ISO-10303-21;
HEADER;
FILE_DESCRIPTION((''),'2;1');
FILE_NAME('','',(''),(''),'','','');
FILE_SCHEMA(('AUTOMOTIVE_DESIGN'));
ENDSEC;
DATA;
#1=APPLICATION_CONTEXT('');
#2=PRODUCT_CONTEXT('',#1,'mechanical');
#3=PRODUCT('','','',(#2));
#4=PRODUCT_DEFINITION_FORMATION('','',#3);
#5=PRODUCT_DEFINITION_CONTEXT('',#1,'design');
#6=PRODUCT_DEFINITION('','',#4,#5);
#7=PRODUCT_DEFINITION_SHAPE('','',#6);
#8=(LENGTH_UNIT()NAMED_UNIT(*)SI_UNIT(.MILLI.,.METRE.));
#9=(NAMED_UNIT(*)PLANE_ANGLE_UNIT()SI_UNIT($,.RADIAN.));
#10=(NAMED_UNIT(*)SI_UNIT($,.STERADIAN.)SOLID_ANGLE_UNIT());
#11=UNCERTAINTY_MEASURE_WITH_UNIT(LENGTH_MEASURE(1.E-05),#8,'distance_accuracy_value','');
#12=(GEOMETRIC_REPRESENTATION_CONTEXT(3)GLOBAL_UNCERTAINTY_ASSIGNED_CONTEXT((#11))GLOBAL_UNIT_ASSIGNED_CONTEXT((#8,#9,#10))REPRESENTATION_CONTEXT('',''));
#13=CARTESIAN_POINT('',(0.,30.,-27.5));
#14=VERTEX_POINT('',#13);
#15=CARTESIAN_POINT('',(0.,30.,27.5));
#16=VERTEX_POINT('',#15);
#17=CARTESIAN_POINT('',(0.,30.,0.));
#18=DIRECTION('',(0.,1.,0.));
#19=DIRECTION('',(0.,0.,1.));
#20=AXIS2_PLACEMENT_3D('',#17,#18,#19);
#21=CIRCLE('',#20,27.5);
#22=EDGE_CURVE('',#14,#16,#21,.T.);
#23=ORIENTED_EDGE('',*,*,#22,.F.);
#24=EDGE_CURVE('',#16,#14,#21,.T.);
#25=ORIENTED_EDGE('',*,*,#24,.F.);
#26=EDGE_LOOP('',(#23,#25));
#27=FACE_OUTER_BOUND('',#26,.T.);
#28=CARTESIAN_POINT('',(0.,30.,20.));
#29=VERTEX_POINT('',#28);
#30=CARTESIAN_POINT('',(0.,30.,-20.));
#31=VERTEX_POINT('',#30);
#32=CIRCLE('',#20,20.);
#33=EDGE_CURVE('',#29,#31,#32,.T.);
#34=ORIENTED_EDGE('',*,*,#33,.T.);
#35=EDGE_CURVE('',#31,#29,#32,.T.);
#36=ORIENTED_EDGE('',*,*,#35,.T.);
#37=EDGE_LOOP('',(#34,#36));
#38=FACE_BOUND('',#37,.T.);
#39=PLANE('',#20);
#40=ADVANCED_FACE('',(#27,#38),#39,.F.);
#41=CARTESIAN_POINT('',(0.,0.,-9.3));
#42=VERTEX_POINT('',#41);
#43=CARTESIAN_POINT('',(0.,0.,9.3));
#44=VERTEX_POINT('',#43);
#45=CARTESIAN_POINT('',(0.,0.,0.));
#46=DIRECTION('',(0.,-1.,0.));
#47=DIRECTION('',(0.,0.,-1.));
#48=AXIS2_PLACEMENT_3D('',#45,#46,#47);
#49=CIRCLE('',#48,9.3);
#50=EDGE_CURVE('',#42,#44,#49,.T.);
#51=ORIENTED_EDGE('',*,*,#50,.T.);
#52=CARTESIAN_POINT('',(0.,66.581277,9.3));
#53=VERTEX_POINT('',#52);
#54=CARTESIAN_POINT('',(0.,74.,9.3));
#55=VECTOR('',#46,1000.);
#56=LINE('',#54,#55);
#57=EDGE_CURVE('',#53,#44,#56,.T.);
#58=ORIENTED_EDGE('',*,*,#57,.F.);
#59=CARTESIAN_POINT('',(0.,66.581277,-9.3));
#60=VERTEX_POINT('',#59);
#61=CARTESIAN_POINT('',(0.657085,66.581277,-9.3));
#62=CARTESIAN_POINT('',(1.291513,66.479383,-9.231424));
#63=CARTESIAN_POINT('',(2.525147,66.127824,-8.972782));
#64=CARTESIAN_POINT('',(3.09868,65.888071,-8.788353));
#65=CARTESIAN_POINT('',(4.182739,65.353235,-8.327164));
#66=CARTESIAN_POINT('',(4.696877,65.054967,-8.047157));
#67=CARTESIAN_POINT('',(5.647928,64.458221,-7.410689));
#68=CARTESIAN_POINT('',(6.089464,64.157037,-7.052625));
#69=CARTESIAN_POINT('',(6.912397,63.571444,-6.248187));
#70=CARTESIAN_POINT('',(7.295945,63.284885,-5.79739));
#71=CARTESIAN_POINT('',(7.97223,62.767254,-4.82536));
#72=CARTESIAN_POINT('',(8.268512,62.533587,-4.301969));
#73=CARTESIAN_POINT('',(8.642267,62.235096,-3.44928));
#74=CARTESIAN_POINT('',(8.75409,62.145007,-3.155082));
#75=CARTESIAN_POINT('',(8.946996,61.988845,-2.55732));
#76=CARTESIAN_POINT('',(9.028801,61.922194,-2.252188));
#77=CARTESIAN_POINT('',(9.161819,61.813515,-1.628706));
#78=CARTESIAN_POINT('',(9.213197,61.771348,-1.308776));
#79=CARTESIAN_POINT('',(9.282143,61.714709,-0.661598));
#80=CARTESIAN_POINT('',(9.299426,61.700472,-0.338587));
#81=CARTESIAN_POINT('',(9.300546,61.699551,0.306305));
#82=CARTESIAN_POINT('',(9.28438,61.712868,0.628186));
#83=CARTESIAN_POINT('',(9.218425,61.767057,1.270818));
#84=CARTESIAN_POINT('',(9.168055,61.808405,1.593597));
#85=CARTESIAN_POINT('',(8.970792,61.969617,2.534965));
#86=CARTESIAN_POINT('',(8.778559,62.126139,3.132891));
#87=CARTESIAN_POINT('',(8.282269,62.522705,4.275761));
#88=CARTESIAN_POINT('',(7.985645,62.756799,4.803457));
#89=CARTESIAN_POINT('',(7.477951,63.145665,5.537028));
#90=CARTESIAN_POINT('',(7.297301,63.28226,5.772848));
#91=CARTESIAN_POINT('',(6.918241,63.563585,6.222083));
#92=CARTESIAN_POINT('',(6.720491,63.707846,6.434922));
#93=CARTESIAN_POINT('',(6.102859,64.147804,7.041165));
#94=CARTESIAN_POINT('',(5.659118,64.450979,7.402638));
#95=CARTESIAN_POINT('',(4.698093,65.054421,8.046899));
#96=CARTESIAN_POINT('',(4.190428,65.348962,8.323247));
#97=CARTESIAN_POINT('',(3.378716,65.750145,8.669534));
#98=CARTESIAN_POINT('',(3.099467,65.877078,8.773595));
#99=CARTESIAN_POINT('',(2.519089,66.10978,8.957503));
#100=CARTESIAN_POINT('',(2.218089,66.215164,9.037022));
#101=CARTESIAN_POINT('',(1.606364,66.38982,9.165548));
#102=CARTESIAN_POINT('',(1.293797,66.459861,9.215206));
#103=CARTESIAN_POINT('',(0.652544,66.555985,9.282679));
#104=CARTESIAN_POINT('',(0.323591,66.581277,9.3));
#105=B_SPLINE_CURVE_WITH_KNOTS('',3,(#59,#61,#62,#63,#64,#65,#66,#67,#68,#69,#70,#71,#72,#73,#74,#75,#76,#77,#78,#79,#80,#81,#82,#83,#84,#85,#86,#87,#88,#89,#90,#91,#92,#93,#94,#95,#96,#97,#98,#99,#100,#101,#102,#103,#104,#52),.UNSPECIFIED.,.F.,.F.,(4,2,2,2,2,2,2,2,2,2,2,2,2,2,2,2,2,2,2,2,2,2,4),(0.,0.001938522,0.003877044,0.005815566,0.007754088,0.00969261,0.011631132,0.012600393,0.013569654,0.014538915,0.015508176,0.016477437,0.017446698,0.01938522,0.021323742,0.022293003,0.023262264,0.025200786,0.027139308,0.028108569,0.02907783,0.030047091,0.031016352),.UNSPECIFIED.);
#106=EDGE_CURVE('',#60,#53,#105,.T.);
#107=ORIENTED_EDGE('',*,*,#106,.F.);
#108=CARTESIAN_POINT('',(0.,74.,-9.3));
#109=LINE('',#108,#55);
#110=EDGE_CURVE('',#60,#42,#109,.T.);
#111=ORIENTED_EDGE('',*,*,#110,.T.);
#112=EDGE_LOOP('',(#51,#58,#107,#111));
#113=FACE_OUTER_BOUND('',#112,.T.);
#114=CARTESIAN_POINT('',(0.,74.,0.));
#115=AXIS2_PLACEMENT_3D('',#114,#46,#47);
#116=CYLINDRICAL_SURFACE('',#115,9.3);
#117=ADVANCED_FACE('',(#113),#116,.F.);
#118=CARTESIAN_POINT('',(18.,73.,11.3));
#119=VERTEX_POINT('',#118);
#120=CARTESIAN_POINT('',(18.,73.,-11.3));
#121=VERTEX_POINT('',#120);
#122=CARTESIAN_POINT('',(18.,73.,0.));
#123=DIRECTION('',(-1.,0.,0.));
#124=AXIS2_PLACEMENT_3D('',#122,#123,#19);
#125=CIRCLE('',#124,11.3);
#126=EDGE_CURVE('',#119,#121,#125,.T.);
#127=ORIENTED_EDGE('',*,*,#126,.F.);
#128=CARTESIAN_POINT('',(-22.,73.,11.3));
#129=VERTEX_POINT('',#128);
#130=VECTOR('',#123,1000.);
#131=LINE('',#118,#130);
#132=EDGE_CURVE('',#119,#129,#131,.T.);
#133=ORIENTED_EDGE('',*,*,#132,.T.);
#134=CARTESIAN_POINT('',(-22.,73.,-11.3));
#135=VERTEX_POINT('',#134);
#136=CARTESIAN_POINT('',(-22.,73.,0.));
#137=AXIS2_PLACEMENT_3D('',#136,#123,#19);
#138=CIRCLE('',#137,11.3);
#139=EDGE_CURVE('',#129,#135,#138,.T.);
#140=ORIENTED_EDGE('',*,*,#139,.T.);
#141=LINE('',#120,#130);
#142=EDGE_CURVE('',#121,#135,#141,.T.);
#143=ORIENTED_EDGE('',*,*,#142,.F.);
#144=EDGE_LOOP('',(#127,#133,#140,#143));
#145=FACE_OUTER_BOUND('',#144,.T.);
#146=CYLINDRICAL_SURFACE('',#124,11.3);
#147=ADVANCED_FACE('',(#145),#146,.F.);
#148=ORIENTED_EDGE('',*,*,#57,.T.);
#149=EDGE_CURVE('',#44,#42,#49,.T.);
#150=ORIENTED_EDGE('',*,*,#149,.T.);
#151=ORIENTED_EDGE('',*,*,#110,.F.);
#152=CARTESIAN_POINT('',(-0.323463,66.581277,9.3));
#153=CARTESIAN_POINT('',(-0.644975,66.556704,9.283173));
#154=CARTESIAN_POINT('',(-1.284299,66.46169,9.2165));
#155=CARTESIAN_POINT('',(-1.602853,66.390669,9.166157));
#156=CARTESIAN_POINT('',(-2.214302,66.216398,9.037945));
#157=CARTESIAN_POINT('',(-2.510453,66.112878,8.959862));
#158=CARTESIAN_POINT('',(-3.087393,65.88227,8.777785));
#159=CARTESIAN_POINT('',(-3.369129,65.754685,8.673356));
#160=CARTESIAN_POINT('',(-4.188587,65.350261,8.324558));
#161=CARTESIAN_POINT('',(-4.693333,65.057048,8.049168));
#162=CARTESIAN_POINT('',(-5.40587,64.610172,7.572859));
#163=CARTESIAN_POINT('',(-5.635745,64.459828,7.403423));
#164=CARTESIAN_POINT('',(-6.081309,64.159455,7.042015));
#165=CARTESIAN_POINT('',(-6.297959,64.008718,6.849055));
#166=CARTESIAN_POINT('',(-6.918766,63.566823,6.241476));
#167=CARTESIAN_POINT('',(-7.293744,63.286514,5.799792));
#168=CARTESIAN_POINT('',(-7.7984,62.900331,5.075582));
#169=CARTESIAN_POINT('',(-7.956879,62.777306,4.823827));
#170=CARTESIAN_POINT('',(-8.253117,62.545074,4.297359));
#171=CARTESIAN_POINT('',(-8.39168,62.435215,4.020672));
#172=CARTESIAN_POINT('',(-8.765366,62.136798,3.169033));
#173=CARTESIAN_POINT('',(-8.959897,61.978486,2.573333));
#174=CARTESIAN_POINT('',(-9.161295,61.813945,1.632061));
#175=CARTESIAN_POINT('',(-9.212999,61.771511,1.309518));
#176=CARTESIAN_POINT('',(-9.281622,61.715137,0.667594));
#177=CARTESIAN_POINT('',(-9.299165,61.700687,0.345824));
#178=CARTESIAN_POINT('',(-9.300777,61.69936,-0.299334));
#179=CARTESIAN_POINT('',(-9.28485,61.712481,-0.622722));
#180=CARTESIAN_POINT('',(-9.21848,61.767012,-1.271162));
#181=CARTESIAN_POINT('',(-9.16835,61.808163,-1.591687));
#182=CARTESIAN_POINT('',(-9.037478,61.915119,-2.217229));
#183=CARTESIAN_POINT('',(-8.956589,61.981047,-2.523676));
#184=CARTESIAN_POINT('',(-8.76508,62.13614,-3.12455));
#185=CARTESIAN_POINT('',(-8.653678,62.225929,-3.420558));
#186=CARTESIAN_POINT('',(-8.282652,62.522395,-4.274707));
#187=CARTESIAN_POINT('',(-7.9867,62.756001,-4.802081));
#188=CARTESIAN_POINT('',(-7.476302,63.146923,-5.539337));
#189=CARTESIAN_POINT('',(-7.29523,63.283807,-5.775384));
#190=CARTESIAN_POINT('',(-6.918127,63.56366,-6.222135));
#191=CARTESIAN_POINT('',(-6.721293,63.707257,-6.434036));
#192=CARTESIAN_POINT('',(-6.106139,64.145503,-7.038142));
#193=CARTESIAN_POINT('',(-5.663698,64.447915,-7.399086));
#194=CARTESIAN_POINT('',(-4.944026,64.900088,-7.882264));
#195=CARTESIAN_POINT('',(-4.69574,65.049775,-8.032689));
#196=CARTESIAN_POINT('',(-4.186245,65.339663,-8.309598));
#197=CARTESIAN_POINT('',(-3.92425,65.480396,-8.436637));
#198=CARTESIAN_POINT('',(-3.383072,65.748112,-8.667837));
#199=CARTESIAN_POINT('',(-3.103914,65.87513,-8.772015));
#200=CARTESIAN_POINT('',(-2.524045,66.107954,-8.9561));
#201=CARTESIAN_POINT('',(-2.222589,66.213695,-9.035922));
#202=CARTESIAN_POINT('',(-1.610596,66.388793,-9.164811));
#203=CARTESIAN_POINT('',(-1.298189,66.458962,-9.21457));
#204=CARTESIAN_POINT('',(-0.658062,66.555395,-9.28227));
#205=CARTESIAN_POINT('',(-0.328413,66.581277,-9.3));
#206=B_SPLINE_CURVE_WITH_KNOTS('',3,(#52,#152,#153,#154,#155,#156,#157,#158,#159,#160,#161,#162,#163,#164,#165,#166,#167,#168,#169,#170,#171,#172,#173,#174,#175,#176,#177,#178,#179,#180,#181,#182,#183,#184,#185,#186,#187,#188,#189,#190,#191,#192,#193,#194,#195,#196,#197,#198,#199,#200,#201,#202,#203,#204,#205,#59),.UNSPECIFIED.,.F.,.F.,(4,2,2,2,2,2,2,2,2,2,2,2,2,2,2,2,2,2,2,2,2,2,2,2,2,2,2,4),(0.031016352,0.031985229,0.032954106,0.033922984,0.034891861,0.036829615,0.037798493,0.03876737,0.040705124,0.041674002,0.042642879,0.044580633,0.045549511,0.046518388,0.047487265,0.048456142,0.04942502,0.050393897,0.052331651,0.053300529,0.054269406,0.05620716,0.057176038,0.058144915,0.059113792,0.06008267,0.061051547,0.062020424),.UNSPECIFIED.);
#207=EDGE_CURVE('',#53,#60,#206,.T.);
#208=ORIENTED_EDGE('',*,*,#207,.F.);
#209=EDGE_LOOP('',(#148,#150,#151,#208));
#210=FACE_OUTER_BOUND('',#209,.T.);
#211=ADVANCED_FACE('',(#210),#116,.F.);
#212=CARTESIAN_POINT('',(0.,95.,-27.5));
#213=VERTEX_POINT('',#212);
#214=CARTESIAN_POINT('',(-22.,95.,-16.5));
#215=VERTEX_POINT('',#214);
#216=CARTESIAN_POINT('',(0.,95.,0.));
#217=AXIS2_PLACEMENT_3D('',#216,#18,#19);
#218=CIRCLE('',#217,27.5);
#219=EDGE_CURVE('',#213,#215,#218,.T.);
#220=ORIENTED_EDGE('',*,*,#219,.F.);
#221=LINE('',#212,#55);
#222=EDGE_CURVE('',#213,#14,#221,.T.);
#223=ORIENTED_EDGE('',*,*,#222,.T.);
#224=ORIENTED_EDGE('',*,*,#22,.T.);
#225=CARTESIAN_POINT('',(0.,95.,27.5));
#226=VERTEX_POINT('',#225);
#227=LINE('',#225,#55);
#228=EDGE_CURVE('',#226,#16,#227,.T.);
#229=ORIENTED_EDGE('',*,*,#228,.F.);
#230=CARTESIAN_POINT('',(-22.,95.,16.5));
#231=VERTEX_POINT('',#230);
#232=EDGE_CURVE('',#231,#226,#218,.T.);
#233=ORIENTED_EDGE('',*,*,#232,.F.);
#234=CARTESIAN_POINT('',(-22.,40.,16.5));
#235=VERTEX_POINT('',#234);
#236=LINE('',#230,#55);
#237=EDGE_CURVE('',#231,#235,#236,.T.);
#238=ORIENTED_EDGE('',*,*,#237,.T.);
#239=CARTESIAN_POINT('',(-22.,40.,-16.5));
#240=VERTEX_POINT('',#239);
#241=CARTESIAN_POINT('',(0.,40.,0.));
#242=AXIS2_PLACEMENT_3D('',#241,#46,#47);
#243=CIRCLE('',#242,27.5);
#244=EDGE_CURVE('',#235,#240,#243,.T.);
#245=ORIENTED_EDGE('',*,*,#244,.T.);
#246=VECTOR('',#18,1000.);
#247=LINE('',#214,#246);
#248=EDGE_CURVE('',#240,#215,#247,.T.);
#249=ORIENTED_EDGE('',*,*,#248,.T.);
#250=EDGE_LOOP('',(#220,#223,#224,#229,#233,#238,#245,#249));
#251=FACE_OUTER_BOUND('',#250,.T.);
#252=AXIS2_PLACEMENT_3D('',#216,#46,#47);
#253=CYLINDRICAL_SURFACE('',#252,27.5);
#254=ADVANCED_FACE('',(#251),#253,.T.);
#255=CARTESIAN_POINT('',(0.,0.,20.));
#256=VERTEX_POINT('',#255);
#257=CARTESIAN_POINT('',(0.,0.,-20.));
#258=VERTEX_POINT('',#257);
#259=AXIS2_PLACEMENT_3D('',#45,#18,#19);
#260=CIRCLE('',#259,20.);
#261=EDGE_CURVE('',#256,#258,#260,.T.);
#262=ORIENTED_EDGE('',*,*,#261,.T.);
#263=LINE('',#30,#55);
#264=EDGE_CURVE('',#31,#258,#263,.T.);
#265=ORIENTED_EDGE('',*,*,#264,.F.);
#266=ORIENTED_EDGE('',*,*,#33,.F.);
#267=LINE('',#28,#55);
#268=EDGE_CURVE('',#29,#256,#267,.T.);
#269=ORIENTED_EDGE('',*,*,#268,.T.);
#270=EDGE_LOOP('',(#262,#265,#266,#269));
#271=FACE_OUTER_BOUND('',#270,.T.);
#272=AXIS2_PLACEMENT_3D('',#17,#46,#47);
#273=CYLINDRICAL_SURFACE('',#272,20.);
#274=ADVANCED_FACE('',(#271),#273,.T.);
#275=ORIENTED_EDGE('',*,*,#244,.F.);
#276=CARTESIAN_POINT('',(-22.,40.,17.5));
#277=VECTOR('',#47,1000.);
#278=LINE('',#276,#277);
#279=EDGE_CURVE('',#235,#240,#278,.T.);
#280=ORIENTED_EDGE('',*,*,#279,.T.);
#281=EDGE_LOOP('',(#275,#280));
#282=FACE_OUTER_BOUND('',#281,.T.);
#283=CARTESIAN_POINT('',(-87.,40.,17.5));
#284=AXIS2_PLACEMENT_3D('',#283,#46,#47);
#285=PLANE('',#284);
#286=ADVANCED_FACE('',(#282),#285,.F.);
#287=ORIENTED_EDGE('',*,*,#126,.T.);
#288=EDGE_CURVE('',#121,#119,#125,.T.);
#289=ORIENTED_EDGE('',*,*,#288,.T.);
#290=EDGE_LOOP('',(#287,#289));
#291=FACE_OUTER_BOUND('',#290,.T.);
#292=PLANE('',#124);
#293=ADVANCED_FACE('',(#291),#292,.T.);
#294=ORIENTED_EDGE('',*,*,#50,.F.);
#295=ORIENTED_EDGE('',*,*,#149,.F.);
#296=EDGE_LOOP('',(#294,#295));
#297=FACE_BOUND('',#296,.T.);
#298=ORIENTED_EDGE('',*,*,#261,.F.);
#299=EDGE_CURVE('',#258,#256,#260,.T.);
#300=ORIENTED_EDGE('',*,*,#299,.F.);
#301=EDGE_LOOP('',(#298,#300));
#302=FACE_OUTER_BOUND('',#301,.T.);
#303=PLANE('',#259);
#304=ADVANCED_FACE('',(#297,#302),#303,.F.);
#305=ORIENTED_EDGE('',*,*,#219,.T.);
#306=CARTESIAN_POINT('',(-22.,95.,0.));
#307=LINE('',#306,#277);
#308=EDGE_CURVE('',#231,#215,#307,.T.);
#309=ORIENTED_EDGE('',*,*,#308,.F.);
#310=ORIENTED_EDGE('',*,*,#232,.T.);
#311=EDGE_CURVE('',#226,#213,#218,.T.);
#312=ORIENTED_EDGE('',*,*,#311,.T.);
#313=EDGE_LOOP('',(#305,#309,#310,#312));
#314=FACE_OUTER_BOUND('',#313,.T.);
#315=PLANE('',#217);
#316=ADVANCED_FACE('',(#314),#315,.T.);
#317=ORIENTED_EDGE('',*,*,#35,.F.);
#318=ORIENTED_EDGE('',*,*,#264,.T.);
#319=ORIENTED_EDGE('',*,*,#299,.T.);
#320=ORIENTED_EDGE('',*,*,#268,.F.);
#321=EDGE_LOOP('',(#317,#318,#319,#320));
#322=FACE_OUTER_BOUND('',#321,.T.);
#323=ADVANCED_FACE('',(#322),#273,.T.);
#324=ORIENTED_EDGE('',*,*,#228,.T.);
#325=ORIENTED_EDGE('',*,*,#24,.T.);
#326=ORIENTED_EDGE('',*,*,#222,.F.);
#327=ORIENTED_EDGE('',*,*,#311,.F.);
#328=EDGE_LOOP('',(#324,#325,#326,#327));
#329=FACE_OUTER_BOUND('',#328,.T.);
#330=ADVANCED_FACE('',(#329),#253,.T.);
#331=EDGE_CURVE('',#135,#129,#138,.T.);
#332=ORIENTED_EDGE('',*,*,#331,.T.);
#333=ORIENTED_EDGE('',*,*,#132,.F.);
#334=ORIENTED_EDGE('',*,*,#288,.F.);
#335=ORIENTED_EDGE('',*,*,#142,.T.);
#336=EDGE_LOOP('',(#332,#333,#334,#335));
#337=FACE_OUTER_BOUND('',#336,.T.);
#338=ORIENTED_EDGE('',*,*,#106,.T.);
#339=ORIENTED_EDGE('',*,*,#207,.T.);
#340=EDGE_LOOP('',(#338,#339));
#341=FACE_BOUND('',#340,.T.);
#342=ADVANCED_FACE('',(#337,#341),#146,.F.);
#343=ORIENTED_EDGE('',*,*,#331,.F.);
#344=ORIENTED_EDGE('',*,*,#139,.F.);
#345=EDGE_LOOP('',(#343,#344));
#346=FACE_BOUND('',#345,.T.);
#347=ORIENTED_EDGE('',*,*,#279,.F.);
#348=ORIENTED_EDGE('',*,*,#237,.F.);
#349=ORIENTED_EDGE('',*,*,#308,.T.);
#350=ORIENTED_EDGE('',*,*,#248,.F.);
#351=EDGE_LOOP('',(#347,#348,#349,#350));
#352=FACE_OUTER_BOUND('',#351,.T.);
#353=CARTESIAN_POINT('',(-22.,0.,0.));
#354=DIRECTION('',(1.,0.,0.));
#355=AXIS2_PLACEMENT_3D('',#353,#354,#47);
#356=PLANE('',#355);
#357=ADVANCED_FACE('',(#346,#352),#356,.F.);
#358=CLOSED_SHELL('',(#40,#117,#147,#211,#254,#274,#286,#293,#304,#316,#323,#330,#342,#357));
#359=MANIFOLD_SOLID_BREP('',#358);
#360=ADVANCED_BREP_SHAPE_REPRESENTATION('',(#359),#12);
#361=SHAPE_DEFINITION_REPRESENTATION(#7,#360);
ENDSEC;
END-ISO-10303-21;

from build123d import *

# Parameters (mm, degrees)
SKETCH1_R           = 20
BOSS_EXTRUDE1_DEPTH = 30
SKETCH2_R           = 27.5
BOSS_EXTRUDE2_DEPTH = 65
CUT_EXTRUDE1_START  = -22
SKETCH3_W           = 35
SKETCH3_H           = 55
CUT_EXTRUDE1_DEPTH  = 65
SKETCH4_R           = 11.3
CUT_EXTRUDE2_DEPTH  = 40
SKETCH5_R           = 9.3
CUT_EXTRUDE3_DEPTH  = 74


with BuildPart() as part:
    # Sketch1 → Boss-Extrude1 (new body)
    with BuildSketch(Plane(origin=(0, 0, 0), x_dir=(1, 0, 0), z_dir=(0, 1, 0))):
        with Locations(Location((0, 0, 0), (0, 0, 270))):
            Circle(SKETCH1_R)
    extrude(amount=BOSS_EXTRUDE1_DEPTH)

    # Sketch2 → Boss-Extrude2 (add)
    with BuildSketch(Plane(origin=(0, 30, 0), x_dir=(1, 0, 0), z_dir=(0, 1, 0))):
        with Locations(Location((0, 0, 0), (0, 0, 270))):
            Circle(SKETCH2_R)
    extrude(amount=BOSS_EXTRUDE2_DEPTH)

    # Sketch3 → Cut-Extrude1 (cut)
    with BuildSketch(Plane(origin=(0, 0, 0), x_dir=(0, 0, -1), z_dir=(1, 0, 0)).offset(CUT_EXTRUDE1_START)):
        with Locations((0, 67.5)):
            Rectangle(SKETCH3_W, SKETCH3_H)
    extrude(amount=-CUT_EXTRUDE1_DEPTH, mode=Mode.SUBTRACT)

    # Sketch4 → Cut-Extrude2 (cut)
    with BuildSketch(Plane.ZY.offset(22)):
        with Locations((0, 73)):
            Circle(SKETCH4_R)
    extrude(amount=-CUT_EXTRUDE2_DEPTH, mode=Mode.SUBTRACT)

    # Sketch5 → Cut-Extrude3 (cut)
    with BuildSketch(Plane.XZ):
        with Locations(Location((0, 0, 0), (0, 0, 270))):
            Circle(SKETCH5_R)
    extrude(amount=-CUT_EXTRUDE3_DEPTH, mode=Mode.SUBTRACT)


solid = part.part
